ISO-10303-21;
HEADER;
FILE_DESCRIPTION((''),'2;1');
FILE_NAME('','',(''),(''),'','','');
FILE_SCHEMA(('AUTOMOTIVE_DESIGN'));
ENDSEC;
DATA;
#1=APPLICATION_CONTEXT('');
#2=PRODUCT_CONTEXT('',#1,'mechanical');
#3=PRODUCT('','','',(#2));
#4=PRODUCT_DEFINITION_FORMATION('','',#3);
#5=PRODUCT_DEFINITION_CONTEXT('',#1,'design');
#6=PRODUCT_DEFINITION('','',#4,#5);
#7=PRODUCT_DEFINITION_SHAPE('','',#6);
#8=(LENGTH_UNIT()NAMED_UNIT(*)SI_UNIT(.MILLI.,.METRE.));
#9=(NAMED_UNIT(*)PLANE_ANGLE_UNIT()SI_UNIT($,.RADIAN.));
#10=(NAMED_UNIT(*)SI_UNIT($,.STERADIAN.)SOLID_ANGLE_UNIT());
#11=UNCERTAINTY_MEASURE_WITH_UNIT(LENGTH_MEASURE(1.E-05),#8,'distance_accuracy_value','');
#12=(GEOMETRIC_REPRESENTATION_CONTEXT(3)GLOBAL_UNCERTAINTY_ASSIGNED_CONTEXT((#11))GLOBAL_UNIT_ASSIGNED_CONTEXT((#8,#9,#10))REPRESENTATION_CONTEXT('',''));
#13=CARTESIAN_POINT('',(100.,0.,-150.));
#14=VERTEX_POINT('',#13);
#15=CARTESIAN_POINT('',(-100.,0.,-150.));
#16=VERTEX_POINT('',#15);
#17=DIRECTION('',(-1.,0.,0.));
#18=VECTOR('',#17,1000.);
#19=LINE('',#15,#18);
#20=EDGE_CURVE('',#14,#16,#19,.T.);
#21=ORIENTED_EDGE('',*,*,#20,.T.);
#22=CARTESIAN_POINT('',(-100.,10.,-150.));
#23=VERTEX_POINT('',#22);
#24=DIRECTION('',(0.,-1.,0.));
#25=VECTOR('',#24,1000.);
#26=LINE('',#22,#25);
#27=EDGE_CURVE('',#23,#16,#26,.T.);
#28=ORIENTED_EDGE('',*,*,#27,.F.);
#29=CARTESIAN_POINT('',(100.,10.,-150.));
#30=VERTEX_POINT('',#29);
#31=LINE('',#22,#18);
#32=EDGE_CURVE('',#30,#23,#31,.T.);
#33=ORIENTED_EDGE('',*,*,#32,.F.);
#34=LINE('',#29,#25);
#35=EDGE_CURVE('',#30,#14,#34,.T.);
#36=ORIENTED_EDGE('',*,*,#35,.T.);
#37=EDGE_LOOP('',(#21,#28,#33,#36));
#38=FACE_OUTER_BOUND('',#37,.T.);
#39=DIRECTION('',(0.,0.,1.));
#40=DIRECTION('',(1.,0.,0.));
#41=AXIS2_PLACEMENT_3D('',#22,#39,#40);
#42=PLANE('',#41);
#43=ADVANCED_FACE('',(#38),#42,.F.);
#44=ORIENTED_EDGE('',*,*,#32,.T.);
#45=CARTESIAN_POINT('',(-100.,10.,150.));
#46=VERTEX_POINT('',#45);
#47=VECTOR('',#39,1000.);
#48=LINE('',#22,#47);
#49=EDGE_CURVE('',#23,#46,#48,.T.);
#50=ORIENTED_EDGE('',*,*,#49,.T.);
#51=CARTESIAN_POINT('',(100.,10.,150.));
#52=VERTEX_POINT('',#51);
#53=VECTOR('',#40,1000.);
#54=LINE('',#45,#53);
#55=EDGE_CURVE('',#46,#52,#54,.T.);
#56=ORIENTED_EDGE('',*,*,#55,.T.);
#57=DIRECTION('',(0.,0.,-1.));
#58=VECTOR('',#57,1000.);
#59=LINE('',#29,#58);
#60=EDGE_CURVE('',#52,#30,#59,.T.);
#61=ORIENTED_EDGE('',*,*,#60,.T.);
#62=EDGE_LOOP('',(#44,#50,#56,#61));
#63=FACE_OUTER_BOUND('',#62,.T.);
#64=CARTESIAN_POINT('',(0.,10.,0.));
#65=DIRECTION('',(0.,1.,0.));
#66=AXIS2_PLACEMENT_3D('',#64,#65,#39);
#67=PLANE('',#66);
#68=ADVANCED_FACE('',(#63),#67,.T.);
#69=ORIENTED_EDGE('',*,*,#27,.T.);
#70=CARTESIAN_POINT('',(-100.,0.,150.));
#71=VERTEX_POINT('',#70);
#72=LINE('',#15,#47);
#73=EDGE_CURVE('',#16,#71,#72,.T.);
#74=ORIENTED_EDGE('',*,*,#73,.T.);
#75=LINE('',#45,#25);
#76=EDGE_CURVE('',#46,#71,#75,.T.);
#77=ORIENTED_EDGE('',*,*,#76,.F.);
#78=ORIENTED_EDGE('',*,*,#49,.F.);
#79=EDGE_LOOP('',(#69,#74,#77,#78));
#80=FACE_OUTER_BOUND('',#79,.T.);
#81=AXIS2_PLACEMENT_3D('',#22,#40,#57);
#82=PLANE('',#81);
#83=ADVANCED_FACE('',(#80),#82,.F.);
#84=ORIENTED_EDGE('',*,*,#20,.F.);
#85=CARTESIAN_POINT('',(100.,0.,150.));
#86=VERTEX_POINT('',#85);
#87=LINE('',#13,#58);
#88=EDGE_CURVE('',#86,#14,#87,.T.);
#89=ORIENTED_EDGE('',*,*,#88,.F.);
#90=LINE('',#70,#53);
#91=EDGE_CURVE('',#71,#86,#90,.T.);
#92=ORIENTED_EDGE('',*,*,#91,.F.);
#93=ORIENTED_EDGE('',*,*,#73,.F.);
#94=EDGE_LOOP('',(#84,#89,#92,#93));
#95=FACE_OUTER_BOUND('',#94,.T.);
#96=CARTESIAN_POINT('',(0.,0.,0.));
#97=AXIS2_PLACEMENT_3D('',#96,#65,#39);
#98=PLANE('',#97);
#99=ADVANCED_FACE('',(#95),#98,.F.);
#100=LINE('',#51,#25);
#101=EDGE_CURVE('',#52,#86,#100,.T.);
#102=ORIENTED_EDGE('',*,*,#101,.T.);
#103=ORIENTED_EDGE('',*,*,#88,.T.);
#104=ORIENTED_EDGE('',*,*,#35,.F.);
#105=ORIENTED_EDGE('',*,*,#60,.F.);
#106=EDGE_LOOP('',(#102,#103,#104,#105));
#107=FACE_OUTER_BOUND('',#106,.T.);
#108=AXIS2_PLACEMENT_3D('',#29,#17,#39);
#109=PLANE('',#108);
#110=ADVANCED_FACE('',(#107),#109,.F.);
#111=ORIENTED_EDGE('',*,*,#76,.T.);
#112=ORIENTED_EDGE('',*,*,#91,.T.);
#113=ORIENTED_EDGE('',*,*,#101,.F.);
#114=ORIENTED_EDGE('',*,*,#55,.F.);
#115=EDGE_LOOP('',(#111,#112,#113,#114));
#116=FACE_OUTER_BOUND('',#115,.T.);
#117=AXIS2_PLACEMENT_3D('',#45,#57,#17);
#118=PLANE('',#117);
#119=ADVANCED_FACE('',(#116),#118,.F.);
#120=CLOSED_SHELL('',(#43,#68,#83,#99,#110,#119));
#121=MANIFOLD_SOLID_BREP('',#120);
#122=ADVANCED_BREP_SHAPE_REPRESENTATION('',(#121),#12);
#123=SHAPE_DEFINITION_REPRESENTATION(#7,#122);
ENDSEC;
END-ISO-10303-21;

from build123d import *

# Parameters (mm, degrees)
SKETCH1_W           = 200
SKETCH1_H           = 300
BOSS_EXTRUDE1_DEPTH = 10


with BuildPart() as part:
    # Sketch1 → Boss-Extrude1 (new body)
    with BuildSketch(Plane(origin=(0, 0, 0), x_dir=(1, 0, 0), z_dir=(0, 1, 0))):
        Rectangle(SKETCH1_W, SKETCH1_H)
    extrude(amount=BOSS_EXTRUDE1_DEPTH)


solid = part.part
